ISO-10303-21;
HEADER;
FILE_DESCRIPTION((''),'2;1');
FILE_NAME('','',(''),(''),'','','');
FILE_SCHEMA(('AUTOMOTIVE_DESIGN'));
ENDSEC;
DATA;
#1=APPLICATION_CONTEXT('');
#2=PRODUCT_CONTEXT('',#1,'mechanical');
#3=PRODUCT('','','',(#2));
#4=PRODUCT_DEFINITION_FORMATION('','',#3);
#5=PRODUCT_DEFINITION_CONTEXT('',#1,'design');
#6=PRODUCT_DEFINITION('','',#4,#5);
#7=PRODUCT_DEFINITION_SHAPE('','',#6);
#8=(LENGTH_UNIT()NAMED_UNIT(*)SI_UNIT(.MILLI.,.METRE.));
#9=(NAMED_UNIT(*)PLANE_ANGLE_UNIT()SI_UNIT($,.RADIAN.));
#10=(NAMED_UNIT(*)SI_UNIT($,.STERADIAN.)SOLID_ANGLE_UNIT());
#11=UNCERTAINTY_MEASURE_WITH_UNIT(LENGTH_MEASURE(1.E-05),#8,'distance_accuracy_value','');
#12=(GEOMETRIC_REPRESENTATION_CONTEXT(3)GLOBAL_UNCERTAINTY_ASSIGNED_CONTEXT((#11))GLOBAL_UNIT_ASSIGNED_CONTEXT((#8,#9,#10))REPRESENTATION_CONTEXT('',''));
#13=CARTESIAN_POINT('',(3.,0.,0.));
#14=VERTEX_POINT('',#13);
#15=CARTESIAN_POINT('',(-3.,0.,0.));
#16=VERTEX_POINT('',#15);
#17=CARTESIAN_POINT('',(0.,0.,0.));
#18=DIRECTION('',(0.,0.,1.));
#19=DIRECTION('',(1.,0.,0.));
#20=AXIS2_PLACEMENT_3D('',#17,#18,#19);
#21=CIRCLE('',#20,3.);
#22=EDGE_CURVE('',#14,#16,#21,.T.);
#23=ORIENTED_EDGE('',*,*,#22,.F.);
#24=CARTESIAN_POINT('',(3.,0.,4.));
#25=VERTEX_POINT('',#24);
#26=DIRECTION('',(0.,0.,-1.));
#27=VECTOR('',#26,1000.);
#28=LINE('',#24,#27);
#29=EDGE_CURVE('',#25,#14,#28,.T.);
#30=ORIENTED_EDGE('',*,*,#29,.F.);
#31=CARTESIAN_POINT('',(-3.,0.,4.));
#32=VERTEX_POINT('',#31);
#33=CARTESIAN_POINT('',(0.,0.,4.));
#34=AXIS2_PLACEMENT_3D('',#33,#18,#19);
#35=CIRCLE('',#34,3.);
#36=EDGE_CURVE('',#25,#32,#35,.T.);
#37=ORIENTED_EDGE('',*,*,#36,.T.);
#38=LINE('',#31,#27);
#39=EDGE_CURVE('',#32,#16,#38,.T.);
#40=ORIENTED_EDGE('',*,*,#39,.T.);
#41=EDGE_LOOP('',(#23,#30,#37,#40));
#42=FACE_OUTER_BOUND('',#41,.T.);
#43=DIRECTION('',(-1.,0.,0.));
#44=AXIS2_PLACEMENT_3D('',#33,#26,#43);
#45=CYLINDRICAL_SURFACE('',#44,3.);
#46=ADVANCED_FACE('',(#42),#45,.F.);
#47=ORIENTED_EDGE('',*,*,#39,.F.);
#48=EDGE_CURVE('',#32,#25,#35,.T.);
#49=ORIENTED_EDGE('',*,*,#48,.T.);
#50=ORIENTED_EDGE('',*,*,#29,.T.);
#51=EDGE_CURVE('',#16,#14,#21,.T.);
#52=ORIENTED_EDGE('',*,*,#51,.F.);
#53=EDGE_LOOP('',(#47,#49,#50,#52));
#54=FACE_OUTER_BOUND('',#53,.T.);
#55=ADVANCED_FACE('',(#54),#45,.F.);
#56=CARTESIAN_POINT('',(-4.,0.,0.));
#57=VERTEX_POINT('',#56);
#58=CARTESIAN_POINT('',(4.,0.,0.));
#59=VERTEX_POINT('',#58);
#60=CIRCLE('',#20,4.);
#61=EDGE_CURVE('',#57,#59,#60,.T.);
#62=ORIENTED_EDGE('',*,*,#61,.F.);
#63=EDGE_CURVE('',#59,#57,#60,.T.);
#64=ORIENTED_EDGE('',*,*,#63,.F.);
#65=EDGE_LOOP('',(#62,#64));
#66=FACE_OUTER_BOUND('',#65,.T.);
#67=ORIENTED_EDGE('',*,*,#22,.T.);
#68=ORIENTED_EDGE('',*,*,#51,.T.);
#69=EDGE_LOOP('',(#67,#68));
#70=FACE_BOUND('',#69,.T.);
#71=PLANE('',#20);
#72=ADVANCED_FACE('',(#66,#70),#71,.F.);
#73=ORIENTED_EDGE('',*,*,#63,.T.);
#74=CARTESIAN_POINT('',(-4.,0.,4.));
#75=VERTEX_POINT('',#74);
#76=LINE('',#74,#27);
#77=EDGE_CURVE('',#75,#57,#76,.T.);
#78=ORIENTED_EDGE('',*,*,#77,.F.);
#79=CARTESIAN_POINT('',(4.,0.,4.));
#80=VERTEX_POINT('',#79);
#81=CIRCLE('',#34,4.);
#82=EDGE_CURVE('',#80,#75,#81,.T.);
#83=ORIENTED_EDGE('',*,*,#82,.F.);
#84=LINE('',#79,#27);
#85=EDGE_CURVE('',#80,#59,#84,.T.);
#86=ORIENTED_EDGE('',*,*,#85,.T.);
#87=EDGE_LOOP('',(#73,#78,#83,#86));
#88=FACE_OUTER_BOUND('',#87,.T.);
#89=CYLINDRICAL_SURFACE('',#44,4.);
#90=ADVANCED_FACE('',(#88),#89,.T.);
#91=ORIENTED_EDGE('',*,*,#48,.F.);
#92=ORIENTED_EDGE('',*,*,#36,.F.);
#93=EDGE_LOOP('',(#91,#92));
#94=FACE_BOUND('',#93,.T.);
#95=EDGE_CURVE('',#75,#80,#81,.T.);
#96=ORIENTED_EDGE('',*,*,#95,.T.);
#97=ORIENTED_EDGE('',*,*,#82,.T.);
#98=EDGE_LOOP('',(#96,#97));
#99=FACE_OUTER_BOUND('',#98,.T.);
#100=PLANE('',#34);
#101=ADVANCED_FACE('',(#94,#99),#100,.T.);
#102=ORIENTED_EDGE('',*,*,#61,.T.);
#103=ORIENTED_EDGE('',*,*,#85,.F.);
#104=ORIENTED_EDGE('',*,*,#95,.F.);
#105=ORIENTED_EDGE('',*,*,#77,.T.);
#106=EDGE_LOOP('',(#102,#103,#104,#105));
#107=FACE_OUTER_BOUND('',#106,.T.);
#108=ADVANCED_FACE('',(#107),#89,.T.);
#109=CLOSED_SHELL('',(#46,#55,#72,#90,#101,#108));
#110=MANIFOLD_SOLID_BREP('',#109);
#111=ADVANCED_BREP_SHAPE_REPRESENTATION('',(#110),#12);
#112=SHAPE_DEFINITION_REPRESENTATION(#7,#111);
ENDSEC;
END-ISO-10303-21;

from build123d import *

# Parameters (mm, degrees)
SKETCH2_R           = 4
SKETCH2_R_2         = 3
BOSS_EXTRUDE1_DEPTH = 4


with BuildPart() as part:
    # Sketch2 → Boss-Extrude1 (new body)
    with BuildSketch(Plane.XY):
        Circle(SKETCH2_R)
        Circle(SKETCH2_R_2, mode=Mode.SUBTRACT)
    extrude(amount=BOSS_EXTRUDE1_DEPTH)


solid = part.part
